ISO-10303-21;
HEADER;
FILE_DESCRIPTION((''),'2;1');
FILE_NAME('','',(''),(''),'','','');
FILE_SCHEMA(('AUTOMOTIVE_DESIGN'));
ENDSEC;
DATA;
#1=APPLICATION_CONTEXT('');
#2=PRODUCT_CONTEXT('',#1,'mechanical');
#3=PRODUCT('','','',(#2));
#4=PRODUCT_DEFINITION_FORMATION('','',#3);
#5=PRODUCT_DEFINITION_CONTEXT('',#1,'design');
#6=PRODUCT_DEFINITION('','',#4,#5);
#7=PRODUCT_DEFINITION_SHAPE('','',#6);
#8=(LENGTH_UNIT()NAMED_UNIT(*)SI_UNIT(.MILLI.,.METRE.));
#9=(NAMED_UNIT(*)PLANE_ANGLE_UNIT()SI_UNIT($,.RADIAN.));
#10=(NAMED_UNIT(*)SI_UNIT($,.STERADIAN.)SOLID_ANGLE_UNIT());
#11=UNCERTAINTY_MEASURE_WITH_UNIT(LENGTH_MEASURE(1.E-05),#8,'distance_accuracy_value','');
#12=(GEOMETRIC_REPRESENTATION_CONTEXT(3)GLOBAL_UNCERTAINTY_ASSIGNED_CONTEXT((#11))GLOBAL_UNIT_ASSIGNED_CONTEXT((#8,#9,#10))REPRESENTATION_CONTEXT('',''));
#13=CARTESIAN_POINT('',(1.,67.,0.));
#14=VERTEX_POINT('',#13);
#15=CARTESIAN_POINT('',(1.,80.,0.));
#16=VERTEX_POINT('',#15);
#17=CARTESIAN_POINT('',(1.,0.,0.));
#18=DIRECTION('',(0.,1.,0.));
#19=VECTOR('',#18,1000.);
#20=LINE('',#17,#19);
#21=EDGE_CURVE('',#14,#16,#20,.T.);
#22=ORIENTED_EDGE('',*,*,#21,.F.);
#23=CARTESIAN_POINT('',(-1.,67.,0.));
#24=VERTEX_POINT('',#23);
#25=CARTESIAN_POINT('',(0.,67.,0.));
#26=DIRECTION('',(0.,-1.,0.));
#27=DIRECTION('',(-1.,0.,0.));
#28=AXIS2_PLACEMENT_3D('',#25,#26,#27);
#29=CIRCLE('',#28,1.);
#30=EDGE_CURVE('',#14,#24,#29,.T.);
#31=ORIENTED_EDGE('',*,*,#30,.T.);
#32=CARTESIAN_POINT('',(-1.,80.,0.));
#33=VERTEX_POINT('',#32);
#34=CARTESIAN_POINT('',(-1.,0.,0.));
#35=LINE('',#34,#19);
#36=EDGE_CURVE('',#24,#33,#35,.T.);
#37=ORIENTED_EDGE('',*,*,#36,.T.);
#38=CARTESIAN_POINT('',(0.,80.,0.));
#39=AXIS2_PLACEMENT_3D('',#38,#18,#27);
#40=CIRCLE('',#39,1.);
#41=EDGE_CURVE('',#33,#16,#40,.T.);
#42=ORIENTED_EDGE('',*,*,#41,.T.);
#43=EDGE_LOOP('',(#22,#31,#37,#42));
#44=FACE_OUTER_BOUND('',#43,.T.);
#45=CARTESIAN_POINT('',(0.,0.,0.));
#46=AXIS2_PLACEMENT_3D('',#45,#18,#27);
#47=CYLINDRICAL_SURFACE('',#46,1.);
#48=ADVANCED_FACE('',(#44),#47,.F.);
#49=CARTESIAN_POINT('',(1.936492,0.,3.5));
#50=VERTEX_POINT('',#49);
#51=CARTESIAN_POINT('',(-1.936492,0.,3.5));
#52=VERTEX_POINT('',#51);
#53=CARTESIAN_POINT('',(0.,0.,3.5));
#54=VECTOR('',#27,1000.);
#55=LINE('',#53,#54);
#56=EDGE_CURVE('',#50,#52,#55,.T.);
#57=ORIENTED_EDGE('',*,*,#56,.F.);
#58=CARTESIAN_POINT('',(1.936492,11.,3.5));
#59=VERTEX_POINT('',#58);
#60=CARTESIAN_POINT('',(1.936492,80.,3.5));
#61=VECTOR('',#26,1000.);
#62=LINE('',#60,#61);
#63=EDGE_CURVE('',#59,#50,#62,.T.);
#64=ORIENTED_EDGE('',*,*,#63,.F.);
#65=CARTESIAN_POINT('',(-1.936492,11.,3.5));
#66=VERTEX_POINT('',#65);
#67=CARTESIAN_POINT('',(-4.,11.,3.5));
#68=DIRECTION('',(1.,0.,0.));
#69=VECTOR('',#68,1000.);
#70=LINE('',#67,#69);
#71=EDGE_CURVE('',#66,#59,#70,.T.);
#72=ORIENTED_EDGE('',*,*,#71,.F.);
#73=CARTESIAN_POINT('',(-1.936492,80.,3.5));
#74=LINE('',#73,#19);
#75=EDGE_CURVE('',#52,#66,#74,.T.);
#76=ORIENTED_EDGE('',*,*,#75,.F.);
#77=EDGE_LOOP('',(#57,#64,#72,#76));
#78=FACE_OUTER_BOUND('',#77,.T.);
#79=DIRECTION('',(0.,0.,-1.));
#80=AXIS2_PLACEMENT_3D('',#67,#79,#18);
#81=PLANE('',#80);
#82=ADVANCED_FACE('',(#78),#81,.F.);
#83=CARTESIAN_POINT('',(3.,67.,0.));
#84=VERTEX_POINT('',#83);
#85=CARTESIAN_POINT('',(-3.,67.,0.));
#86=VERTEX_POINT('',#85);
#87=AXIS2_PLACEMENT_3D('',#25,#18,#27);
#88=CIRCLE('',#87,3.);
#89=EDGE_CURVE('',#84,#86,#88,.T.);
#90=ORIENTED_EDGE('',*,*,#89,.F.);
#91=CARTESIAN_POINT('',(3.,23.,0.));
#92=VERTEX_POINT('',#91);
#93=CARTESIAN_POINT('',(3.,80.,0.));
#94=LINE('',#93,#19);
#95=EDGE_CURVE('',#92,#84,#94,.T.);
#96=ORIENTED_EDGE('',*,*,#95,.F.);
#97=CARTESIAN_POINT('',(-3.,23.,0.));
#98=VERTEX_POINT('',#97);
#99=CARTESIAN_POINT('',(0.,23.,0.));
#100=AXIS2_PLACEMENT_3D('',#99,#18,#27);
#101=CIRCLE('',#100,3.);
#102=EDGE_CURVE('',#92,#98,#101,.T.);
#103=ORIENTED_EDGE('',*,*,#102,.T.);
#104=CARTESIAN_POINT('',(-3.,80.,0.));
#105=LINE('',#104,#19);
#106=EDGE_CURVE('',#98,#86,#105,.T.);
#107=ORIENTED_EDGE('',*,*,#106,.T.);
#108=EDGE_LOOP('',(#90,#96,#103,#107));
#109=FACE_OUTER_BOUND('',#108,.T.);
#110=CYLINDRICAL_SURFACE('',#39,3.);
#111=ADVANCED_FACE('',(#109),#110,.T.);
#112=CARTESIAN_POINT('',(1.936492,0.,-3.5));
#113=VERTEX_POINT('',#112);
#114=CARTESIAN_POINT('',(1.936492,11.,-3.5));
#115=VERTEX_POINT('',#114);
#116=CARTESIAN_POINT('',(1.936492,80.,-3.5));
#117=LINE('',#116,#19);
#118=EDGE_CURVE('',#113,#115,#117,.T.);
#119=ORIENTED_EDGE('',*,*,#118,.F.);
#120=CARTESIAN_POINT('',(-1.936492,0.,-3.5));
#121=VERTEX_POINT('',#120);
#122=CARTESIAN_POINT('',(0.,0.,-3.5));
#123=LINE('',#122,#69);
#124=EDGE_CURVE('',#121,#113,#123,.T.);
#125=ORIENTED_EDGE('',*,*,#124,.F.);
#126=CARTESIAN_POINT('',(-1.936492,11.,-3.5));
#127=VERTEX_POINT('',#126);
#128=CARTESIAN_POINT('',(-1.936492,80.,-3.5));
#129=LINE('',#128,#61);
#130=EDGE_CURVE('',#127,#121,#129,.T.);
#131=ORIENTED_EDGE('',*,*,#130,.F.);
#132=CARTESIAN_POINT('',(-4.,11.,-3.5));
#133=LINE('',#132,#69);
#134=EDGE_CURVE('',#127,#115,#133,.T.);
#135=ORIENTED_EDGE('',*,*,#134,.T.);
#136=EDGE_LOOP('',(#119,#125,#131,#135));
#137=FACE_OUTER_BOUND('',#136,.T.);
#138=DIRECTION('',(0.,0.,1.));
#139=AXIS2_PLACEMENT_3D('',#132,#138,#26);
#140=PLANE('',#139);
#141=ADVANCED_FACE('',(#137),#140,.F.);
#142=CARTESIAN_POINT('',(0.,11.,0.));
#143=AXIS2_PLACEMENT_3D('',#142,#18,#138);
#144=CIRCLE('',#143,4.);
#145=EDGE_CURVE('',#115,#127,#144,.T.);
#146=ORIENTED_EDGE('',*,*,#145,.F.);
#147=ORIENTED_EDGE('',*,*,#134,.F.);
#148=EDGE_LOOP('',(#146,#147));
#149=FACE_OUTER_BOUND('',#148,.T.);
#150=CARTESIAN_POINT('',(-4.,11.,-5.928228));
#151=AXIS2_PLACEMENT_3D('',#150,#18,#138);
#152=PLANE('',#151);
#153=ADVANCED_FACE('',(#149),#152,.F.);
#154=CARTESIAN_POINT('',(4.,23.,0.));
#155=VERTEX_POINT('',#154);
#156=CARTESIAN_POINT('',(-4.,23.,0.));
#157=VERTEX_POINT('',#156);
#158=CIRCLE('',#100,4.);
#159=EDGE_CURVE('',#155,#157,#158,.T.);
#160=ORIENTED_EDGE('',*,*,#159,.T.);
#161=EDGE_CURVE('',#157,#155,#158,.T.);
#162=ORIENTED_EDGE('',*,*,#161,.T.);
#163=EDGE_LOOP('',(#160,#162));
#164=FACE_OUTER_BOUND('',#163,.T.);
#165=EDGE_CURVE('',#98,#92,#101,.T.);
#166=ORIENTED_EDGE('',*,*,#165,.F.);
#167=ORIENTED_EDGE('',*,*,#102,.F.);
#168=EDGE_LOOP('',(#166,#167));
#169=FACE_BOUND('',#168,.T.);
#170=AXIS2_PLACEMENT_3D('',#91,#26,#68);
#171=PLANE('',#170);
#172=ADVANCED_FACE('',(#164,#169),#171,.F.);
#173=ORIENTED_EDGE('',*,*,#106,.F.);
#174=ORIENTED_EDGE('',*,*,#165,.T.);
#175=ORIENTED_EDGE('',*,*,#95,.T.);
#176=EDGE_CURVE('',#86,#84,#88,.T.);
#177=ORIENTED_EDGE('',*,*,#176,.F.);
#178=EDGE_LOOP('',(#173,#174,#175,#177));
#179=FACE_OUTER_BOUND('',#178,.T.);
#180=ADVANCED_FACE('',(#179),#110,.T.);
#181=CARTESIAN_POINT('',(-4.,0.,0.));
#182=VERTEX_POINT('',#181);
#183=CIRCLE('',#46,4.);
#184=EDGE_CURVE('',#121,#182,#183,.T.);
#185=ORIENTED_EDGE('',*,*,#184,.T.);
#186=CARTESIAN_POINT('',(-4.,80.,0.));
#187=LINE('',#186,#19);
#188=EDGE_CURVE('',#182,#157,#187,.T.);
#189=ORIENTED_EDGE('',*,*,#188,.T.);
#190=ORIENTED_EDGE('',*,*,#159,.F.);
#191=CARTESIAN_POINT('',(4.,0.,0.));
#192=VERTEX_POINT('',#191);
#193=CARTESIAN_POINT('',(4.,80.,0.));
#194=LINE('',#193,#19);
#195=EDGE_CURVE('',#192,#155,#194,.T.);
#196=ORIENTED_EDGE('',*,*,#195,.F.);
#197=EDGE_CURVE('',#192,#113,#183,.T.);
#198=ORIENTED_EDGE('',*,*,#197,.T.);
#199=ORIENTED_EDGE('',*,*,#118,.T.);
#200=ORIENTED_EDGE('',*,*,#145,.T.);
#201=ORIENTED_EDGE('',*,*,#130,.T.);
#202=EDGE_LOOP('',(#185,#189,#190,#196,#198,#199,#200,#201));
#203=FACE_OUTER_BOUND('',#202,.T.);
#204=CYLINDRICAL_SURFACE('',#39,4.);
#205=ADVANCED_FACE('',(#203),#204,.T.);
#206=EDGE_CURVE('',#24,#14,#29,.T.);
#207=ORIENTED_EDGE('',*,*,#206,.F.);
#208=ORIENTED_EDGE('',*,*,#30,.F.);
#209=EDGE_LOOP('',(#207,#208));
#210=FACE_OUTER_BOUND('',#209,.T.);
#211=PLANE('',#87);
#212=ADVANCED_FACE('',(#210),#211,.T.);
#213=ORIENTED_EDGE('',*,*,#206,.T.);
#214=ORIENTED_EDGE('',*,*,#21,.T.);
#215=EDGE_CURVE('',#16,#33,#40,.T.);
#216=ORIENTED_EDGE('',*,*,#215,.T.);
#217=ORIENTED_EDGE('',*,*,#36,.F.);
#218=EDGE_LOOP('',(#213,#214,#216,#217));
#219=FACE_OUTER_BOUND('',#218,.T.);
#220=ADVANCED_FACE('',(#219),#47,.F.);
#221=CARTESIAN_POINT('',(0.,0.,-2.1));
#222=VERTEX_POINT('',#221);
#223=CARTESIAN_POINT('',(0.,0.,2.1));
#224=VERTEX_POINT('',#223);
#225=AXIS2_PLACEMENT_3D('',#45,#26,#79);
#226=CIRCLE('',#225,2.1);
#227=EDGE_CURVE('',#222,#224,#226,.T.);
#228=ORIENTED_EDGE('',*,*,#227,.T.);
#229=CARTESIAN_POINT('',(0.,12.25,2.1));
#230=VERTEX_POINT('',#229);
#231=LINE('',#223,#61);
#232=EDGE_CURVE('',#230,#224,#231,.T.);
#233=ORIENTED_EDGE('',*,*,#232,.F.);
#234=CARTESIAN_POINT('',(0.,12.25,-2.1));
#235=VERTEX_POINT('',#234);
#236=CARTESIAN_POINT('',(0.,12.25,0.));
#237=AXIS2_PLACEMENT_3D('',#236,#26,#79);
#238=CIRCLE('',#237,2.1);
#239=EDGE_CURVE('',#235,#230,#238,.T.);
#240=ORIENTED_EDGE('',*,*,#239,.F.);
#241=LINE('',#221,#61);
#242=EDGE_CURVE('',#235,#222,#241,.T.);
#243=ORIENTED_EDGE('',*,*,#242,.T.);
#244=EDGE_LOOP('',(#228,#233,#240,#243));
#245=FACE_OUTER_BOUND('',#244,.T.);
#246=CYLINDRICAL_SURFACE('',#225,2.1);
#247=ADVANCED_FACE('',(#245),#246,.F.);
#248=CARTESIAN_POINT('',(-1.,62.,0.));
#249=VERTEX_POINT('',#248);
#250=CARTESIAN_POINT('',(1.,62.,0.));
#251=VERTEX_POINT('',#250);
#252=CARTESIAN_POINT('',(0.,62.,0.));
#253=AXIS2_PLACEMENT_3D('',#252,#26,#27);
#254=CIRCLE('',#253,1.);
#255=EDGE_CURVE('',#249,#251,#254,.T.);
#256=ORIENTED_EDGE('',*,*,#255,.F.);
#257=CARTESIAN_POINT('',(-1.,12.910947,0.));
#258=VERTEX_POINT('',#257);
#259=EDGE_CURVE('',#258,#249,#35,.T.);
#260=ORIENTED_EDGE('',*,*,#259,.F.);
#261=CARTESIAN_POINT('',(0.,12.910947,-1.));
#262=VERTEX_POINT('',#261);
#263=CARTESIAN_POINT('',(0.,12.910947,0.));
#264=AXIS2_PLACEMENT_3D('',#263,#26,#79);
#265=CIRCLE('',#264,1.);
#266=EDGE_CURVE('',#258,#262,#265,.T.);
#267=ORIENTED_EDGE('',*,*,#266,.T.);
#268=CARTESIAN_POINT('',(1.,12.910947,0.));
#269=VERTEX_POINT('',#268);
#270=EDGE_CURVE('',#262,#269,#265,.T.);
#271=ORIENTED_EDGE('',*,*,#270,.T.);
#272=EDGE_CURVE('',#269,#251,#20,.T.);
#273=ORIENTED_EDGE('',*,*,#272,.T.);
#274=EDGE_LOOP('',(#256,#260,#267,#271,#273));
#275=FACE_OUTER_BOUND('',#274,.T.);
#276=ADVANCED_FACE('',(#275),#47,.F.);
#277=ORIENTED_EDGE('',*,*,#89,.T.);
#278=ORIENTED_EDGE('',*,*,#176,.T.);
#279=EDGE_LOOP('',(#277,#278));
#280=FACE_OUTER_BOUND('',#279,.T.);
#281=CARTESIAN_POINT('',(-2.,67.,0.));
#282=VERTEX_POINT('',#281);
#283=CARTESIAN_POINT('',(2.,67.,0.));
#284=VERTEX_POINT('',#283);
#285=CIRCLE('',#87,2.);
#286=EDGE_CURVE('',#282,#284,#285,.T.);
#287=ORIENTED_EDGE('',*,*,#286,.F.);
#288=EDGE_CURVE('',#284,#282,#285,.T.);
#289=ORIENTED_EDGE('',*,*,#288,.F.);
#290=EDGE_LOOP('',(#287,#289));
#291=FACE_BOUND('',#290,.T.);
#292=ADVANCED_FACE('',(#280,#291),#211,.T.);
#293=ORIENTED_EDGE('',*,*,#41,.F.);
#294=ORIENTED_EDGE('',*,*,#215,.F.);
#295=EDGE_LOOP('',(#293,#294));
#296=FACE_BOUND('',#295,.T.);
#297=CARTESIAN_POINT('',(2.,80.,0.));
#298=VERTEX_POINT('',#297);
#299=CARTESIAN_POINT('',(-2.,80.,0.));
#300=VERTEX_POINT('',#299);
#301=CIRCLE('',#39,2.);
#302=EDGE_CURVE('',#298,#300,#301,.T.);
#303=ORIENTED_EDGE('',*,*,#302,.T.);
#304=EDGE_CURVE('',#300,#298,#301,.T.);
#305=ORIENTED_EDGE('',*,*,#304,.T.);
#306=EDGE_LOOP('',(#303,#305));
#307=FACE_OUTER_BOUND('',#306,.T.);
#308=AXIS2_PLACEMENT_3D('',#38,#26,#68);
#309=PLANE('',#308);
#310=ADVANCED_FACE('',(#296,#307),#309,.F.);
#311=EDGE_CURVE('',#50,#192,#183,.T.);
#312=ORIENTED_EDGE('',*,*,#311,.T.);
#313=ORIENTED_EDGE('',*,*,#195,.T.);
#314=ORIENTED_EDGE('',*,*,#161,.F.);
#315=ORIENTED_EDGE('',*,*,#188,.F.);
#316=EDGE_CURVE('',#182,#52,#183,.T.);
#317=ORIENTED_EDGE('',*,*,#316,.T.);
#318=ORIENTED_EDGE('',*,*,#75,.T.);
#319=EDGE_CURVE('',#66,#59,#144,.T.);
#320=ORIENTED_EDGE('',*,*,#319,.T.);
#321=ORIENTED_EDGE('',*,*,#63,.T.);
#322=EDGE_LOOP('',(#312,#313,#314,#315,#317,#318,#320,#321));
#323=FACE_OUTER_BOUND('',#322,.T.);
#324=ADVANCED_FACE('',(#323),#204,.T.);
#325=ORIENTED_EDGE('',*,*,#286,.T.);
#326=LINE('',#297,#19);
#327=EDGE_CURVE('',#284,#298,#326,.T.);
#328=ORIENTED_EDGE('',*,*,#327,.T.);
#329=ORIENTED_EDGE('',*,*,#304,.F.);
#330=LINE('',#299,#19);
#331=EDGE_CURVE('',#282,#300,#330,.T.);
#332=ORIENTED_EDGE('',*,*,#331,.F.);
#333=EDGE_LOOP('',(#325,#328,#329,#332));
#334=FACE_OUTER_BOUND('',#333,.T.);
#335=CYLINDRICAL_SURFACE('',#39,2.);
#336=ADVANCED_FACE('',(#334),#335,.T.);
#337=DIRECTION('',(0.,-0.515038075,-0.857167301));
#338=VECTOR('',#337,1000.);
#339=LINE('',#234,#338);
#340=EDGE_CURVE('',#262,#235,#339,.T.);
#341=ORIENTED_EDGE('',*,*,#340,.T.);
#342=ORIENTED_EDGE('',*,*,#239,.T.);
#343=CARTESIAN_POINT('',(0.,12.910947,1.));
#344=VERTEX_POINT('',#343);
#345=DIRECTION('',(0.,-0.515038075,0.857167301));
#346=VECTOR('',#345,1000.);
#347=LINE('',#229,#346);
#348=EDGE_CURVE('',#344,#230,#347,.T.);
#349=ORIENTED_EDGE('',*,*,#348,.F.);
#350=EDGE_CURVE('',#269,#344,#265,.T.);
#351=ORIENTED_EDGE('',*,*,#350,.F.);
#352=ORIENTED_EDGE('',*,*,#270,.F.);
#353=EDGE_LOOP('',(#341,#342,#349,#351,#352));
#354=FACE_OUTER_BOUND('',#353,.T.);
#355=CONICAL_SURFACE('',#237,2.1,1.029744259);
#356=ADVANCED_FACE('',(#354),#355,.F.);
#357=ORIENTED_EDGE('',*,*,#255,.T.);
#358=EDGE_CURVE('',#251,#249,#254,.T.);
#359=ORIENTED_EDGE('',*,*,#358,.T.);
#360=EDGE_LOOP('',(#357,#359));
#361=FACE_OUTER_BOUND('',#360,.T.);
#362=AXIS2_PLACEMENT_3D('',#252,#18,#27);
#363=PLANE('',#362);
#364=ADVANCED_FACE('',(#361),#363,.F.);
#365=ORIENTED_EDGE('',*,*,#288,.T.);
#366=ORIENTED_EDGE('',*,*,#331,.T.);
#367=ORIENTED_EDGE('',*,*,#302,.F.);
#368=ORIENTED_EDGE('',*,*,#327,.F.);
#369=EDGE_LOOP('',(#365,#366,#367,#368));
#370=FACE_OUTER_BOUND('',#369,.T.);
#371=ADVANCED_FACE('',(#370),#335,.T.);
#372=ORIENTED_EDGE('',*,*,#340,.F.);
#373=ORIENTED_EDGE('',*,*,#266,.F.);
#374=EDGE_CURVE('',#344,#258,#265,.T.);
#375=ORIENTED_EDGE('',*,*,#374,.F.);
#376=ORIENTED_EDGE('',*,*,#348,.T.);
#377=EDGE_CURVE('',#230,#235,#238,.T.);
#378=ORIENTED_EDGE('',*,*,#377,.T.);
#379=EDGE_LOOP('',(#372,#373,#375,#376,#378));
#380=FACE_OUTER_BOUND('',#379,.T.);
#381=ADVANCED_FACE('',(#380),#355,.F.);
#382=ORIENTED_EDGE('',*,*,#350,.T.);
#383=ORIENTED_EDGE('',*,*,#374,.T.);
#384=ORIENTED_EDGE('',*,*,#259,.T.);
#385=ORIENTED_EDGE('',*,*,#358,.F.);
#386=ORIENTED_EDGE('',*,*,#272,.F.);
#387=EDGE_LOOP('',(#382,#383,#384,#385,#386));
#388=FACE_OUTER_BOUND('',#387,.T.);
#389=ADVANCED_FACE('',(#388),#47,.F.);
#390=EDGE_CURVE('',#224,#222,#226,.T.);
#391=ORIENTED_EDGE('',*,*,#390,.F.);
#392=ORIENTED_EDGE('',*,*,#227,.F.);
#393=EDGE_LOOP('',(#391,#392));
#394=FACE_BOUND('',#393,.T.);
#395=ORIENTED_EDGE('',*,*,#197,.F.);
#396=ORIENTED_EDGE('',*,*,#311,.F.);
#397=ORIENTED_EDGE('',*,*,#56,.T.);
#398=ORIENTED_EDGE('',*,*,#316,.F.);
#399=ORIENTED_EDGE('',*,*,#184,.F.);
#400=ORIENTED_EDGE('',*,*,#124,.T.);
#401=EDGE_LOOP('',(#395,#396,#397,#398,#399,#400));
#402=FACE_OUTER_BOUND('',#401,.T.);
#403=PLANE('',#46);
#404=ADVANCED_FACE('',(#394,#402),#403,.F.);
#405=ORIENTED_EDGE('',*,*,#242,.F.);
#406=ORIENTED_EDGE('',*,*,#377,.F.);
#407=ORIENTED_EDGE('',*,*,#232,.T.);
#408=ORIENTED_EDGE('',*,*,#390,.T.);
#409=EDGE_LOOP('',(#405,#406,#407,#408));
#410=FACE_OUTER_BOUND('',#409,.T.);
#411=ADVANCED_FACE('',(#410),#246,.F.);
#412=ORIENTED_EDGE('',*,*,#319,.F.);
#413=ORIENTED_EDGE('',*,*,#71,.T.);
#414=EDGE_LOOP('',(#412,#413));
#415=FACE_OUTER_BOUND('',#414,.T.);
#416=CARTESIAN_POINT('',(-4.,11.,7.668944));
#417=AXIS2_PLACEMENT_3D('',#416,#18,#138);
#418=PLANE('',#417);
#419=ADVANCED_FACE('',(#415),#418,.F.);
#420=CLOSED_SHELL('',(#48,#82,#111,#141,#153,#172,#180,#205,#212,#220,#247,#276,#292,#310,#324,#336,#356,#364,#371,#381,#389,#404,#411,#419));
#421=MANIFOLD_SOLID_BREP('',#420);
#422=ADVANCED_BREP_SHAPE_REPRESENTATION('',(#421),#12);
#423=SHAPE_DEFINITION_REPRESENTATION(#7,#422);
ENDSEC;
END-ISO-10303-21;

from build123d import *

# Parameters (mm, degrees)
SKETCH5_R                  = 1
CUT_EXTRUDE2_DEPTH         = 81.199750623
M5X0_75_TAPPED_HOLE1_D     = 4.2
M5X0_75_TAPPED_HOLE1_DEPTH = 12.25
M5X0_75_TAPPED_HOLE1_TIP   = 1.2618073
CUT_EXTRUDE3_DEPTH         = 81.199750623
CUT_EXTRUDE3_DEPTH_BACK    = 81.199750623
SKETCH6_W                  = 4.168944331
SKETCH6_H                  = 22.175025747
SKETCH6_W_2                = 2.42822795
SKETCH7_R                  = 3
BOSS_EXTRUDE1_DEPTH        = 5


with BuildPart() as part:
    # Sketch1 → Revolve1 (revolve)
    with BuildSketch(Plane.XY, mode=Mode.PRIVATE) as revolve1_sk:
        Polygon((3, 23), (4, 23), (4, 0), (0, 0), (0, 80), (2, 80), (2, 62), (3, 62), align=None)
    revolve(revolve1_sk.sketch.rotate(Axis((0, 80, 0), (0, -1, 0)), 180), axis=Axis((0, 80, 0), (0, -1, 0)))

    # Sketch5 → Cut-Extrude2 (cut, through all)
    with BuildSketch(Plane(origin=(0, 80, 0), x_dir=(1, 0, 0), z_dir=(0, 1, 0))):
        with Locations(Location((0, 0, 0), (0, 0, 180))):
            Circle(SKETCH5_R)
    extrude(amount=-CUT_EXTRUDE2_DEPTH, mode=Mode.SUBTRACT)

    # M5x0.75 Tapped Hole1
    with Locations(Plane(origin=(0, 0, 0), x_dir=(-1, 0, 0), z_dir=(0, -1, 0))):
        with Locations((0, 0)):
            Hole(M5X0_75_TAPPED_HOLE1_D / 2, depth=M5X0_75_TAPPED_HOLE1_DEPTH)
            with Locations((0, 0, -(M5X0_75_TAPPED_HOLE1_DEPTH + M5X0_75_TAPPED_HOLE1_TIP / 2))):  # 118° drill point
                Cone(0, M5X0_75_TAPPED_HOLE1_D / 2, M5X0_75_TAPPED_HOLE1_TIP, mode=Mode.SUBTRACT)

    # Sketch6 → Cut-Extrude3 (cut, two sides: drawn at the far end of the back side and taken through both)
    with BuildSketch(Plane(origin=(0, 0, 0), x_dir=(0, 0, -1), z_dir=(1, 0, 0)).offset(-CUT_EXTRUDE3_DEPTH_BACK)):
        with Locations((-5.584472166, -0.087512874)):
            Rectangle(SKETCH6_W, SKETCH6_H)
        with Locations((4.714113975, -0.087512874)):
            Rectangle(SKETCH6_W_2, SKETCH6_H)
    extrude(amount=CUT_EXTRUDE3_DEPTH + CUT_EXTRUDE3_DEPTH_BACK, mode=Mode.SUBTRACT)

    # Sketch7 → Boss-Extrude1 (add)
    with BuildSketch(Plane(origin=(0, 62, 0), x_dir=(1, 0, 0), z_dir=(0, 1, 0))):
        with Locations(Location((0, 0, 0), (0, 0, 180))):
            Circle(SKETCH7_R)
    extrude(amount=BOSS_EXTRUDE1_DEPTH)


solid = part.part
